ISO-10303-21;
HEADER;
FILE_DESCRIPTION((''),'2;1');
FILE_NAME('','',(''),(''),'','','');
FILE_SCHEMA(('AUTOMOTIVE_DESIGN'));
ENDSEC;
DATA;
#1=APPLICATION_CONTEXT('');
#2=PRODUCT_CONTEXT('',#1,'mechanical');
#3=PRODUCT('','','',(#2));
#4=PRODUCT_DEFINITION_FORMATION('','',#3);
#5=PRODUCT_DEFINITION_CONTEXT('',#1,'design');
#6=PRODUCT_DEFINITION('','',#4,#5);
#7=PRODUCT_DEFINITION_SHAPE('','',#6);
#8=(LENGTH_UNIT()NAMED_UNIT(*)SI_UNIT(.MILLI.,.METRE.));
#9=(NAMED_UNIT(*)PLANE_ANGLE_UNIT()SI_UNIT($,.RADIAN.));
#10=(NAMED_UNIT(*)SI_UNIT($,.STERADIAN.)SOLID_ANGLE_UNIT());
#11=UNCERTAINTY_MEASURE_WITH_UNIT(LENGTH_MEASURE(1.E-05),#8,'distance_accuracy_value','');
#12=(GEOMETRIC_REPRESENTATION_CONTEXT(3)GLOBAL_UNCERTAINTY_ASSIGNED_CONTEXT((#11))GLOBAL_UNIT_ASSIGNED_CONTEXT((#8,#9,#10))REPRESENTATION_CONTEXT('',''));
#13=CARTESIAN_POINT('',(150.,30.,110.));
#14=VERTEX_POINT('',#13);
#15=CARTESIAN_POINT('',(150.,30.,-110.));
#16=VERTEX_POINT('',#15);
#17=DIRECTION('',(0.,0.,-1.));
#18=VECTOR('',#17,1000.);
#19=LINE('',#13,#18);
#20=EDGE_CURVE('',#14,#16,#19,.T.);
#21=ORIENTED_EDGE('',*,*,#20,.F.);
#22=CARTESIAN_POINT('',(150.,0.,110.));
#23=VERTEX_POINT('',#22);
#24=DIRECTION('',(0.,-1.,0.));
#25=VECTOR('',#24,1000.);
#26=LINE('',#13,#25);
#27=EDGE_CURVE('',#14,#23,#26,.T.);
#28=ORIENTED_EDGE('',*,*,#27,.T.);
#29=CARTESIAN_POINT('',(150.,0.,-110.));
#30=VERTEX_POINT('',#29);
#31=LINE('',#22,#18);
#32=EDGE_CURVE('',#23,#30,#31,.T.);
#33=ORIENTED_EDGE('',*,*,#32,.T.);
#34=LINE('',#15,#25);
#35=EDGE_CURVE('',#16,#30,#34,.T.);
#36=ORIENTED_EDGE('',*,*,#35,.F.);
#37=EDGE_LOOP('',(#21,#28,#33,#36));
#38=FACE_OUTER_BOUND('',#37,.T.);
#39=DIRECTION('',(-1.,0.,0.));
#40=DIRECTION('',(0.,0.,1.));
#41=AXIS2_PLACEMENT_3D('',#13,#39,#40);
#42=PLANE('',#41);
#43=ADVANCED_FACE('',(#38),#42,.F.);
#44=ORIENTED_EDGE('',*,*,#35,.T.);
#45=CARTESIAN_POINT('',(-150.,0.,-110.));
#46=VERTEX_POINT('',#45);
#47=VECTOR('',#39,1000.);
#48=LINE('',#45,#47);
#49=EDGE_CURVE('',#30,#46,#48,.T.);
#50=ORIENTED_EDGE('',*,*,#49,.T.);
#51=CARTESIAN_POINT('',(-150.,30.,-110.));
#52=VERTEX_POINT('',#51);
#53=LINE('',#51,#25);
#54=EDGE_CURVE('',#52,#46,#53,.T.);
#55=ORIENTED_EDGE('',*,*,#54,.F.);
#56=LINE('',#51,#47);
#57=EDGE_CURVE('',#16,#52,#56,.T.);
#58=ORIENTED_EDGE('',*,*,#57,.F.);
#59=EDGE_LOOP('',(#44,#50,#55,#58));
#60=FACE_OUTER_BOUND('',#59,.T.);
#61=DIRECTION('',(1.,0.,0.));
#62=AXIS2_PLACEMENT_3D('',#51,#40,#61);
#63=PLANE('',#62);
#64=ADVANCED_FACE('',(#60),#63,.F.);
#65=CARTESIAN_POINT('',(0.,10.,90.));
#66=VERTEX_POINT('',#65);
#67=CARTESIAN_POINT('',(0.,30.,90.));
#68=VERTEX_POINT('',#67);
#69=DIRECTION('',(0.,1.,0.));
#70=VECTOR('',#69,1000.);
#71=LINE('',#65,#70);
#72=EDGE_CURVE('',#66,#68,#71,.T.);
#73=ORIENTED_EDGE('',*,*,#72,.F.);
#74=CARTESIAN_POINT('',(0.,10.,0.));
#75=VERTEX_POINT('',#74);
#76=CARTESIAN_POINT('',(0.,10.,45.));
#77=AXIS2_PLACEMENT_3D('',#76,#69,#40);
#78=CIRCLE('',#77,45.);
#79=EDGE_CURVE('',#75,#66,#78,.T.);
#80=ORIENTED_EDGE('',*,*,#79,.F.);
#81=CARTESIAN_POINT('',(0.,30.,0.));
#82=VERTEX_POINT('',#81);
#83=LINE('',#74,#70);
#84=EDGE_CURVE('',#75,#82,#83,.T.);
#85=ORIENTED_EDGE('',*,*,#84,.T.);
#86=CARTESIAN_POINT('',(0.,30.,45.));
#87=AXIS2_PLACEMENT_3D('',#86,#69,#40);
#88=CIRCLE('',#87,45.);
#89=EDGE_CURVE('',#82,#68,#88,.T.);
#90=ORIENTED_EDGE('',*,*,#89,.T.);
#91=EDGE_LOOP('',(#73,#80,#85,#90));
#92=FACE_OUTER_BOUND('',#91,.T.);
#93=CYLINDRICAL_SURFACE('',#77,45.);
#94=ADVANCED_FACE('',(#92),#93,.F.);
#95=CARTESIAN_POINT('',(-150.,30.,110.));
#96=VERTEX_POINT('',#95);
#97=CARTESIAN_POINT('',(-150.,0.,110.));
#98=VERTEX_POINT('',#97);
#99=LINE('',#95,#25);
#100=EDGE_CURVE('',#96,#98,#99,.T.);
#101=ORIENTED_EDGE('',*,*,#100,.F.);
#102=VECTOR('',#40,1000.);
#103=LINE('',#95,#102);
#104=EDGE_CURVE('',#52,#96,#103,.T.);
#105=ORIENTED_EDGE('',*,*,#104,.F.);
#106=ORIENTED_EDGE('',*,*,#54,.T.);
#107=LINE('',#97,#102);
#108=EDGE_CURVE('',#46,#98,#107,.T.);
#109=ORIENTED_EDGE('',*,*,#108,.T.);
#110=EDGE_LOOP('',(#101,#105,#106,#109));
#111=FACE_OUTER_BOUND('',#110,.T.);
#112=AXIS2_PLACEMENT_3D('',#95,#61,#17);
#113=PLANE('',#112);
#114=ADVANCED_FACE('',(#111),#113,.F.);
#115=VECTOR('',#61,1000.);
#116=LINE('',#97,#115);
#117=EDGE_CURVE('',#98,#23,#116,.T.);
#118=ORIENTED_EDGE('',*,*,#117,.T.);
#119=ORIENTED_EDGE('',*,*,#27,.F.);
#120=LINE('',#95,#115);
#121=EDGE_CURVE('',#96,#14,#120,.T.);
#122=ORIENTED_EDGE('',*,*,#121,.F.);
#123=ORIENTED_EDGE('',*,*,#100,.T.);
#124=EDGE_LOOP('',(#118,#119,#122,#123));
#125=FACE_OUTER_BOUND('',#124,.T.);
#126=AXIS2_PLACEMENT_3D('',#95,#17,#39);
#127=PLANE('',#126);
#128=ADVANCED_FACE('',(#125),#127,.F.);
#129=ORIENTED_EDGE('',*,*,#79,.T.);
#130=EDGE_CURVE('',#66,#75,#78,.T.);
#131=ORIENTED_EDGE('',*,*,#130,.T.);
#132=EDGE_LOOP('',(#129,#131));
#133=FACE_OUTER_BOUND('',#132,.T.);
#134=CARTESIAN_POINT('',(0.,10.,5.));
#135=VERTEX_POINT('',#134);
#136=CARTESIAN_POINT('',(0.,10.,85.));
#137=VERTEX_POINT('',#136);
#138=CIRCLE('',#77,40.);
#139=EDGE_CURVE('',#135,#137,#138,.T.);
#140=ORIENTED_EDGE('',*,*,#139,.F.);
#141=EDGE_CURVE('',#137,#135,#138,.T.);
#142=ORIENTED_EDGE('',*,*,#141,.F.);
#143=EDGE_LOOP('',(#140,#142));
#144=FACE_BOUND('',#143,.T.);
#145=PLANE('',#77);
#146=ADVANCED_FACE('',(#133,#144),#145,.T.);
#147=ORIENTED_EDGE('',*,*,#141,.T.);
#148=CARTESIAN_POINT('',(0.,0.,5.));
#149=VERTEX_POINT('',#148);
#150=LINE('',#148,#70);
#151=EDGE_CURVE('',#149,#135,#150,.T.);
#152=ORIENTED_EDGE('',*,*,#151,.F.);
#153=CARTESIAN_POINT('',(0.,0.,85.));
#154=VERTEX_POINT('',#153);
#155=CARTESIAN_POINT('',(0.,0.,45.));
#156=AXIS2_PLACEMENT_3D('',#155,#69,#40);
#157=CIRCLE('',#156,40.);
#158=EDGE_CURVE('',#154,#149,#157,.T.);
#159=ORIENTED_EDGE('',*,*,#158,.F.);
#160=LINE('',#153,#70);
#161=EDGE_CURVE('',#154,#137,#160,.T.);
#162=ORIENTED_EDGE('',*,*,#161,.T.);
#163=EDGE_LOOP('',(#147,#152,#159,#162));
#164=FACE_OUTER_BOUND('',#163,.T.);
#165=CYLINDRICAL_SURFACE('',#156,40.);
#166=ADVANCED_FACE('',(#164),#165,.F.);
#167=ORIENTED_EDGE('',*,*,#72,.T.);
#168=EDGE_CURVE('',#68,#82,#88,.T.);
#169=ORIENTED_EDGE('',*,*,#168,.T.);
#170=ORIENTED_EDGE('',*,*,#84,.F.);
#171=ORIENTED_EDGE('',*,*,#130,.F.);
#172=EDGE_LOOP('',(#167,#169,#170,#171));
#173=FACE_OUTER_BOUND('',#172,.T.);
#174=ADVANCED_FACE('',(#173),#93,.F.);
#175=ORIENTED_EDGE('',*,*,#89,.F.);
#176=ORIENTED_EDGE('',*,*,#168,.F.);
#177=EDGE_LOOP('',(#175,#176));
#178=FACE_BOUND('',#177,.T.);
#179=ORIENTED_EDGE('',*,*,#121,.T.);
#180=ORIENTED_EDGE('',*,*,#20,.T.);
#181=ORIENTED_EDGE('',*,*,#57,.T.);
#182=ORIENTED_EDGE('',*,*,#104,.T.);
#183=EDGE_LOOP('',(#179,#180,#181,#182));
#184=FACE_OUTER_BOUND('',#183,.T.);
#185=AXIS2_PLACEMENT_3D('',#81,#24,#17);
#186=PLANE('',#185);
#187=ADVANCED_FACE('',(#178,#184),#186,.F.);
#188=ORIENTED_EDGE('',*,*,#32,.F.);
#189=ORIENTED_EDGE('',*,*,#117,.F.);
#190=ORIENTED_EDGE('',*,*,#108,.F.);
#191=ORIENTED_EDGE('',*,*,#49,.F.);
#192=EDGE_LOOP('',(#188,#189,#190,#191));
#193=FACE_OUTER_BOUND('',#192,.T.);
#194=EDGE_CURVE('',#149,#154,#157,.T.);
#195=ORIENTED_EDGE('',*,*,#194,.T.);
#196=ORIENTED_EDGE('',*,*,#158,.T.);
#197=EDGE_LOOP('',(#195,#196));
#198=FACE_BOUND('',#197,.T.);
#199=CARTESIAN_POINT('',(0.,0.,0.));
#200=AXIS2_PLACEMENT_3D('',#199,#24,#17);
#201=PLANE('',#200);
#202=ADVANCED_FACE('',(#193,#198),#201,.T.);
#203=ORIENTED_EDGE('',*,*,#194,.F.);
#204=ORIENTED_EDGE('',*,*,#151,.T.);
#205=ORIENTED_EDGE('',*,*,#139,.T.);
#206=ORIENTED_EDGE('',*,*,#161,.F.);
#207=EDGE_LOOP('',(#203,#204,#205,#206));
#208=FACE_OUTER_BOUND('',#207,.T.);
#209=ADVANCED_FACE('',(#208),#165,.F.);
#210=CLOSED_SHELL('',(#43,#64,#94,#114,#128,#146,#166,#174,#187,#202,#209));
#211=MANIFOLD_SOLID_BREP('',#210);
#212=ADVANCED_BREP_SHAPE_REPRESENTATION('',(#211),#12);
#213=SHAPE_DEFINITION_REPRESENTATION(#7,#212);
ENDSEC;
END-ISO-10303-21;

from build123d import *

# Parameters (mm, degrees)
SKETCH_1_W          = 300
SKETCH_1_H          = 220
EXTRUDE_1_DEPTH     = 30
SKETCH_2_R          = 45
CUT_EXTRUDE_1_DEPTH = 20
SKETCH_3_R          = 40
CUT_EXTRUDE_2_DEPTH = 189.414436814


with BuildPart() as part:
    # 草图1 → 凸台-拉伸1 (new body)
    with BuildSketch(Plane(origin=(0, 0, 0), x_dir=(1, 0, 0), z_dir=(0, 1, 0))):
        Rectangle(SKETCH_1_W, SKETCH_1_H)
    extrude(amount=EXTRUDE_1_DEPTH)

    # 草图2 → 切除-拉伸1 (cut)
    with BuildSketch(Plane(origin=(0, 30, 0), x_dir=(1, 0, 0), z_dir=(0, 1, 0))):
        with Locations(Location((0, -45, 0), (0, 0, 270))):
            Circle(SKETCH_2_R)
    extrude(amount=-CUT_EXTRUDE_1_DEPTH, mode=Mode.SUBTRACT)

    # 草图3 → 切除-拉伸2 (cut, through all)
    with BuildSketch(Plane(origin=(0, 30, 0), x_dir=(1, 0, 0), z_dir=(0, 1, 0))):
        with Locations(Location((0, -45, 0), (0, 0, 270))):
            Circle(SKETCH_3_R)
    extrude(amount=-CUT_EXTRUDE_2_DEPTH, mode=Mode.SUBTRACT)


solid = part.part
